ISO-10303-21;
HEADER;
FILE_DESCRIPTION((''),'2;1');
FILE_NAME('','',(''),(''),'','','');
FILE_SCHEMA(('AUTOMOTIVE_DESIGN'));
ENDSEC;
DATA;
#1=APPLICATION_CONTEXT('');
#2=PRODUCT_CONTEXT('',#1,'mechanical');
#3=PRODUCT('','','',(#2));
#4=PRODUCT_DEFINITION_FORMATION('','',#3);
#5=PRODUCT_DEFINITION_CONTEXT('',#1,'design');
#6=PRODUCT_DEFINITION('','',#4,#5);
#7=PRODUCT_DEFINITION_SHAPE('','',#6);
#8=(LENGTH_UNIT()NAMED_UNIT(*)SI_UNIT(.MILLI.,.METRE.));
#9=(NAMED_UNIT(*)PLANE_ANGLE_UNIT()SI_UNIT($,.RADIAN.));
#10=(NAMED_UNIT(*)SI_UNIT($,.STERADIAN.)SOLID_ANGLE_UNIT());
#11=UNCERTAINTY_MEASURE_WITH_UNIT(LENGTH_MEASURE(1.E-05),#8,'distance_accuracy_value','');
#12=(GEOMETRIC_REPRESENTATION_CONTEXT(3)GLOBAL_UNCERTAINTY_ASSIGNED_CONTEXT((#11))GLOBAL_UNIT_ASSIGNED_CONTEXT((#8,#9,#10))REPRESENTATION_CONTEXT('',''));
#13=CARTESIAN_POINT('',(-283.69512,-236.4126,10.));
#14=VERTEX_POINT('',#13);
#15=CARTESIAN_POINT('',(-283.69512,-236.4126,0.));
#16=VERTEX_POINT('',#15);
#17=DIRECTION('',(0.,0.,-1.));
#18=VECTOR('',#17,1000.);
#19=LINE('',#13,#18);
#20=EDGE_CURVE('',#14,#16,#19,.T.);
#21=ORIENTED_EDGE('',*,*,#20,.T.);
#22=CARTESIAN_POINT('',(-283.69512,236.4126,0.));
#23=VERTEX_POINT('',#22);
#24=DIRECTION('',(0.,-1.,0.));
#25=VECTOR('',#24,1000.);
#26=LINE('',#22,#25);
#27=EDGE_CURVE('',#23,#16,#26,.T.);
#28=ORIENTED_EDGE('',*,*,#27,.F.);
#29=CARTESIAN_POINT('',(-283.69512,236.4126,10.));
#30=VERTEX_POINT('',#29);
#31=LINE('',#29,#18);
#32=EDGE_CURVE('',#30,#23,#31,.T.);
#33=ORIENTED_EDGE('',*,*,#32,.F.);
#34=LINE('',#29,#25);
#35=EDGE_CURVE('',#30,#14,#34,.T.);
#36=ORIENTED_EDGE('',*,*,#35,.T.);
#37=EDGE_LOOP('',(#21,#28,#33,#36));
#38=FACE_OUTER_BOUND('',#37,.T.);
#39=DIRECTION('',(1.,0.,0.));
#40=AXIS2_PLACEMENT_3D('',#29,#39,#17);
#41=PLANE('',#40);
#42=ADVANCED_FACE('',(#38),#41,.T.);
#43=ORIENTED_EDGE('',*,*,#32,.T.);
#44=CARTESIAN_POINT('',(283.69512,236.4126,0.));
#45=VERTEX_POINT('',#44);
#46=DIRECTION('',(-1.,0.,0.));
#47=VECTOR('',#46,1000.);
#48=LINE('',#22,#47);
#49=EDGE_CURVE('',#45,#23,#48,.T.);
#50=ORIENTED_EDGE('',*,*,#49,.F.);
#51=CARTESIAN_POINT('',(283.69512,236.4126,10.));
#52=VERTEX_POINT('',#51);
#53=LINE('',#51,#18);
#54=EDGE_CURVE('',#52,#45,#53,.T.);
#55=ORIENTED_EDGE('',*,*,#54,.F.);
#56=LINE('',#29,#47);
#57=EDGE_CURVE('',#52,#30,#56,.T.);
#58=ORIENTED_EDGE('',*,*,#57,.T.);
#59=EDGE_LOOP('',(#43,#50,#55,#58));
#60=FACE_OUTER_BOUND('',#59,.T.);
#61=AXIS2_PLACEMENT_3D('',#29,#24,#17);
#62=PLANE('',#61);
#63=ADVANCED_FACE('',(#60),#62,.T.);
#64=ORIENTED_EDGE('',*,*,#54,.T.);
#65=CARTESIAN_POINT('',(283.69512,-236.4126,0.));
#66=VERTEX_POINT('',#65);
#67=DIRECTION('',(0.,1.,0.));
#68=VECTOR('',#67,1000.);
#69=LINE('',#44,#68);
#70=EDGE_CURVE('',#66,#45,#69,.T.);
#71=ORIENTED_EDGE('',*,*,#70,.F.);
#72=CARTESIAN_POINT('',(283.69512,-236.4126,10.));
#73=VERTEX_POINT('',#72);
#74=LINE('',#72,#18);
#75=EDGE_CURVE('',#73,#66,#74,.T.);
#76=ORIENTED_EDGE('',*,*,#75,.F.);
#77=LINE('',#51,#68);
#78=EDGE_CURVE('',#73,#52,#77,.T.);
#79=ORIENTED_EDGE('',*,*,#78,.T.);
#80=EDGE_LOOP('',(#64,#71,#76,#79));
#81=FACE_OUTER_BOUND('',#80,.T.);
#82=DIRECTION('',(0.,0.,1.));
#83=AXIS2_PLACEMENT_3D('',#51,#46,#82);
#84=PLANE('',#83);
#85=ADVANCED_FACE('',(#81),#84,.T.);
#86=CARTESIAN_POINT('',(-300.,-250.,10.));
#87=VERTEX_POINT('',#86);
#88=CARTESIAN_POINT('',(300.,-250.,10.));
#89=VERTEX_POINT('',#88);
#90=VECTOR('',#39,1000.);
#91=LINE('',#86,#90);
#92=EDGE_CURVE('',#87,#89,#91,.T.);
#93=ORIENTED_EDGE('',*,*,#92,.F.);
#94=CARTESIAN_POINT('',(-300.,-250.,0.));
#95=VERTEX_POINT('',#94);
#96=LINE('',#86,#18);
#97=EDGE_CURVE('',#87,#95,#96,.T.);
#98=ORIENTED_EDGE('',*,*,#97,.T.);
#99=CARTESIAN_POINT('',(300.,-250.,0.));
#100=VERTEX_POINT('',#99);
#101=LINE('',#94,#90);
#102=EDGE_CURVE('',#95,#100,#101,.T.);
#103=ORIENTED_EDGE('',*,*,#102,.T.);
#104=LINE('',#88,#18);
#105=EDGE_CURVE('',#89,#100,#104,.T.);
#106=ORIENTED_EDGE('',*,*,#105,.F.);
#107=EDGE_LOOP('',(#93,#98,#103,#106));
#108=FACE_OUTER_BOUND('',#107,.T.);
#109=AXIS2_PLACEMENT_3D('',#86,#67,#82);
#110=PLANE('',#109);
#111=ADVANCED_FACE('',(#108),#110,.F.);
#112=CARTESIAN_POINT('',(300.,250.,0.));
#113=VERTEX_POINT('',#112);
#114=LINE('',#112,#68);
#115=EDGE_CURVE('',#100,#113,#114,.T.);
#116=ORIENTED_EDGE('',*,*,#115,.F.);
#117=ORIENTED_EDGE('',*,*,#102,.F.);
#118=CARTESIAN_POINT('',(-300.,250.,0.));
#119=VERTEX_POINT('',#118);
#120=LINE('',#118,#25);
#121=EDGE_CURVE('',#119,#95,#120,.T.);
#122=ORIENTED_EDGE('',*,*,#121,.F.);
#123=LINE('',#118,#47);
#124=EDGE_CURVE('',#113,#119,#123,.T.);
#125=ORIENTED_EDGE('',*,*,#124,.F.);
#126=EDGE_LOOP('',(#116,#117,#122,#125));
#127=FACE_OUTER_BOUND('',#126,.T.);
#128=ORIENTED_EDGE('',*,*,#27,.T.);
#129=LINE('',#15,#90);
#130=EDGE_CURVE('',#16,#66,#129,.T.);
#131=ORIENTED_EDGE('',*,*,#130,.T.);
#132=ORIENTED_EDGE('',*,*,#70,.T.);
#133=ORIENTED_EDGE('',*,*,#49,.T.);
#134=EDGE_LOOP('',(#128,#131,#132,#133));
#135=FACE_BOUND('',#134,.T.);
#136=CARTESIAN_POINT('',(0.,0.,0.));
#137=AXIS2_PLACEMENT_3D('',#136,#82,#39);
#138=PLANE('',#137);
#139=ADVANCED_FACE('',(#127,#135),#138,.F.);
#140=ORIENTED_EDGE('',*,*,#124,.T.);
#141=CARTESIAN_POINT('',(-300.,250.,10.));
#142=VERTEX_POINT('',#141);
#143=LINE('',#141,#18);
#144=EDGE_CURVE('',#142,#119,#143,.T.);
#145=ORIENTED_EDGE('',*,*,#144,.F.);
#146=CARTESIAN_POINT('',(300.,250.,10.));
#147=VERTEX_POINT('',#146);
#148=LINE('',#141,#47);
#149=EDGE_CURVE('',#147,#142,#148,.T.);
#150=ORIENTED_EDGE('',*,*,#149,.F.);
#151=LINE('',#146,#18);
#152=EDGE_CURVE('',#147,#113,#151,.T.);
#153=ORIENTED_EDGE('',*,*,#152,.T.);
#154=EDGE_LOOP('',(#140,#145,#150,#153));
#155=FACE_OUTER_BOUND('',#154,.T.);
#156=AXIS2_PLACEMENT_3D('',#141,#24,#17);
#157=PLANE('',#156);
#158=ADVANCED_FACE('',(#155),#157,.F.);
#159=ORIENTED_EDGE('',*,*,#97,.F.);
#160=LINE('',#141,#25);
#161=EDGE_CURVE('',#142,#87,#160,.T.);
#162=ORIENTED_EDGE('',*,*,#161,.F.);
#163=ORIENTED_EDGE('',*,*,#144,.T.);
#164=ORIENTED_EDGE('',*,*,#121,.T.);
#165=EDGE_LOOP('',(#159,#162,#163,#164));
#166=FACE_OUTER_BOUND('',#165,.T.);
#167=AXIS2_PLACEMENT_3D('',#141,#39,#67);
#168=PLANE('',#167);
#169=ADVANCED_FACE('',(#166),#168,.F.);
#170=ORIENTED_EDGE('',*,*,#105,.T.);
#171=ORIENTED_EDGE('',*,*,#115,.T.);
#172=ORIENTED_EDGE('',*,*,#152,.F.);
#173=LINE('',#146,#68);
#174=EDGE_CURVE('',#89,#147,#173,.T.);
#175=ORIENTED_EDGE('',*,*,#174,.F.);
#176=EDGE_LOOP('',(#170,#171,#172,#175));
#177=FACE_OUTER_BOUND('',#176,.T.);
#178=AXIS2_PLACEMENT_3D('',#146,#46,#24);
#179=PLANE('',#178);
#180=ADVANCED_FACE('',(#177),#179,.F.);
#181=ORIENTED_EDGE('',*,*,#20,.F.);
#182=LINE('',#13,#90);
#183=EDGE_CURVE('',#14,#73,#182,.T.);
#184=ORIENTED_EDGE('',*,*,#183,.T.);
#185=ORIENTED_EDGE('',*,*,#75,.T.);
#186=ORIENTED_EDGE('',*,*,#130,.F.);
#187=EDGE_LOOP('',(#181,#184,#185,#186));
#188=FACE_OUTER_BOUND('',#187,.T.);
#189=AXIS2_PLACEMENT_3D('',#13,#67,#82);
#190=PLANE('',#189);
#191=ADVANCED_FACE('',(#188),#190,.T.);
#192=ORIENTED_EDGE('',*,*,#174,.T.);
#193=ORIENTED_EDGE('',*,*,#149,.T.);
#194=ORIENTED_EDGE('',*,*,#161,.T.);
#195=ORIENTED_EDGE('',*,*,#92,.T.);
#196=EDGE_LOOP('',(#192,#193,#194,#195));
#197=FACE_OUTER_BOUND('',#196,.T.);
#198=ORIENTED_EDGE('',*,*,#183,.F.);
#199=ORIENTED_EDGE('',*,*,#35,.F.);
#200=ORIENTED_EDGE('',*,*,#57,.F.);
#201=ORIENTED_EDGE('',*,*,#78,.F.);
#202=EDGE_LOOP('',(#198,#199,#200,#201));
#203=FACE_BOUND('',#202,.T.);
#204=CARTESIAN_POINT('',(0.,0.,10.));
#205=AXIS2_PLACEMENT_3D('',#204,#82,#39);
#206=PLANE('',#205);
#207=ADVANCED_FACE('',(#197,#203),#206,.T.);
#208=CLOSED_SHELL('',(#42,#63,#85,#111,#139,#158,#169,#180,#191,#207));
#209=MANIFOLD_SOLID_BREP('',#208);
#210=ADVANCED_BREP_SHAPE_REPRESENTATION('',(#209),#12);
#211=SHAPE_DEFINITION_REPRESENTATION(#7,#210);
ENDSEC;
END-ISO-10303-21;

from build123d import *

# Parameters (mm, degrees)
SKETCH1_W           = 600
SKETCH1_H           = 500
SKETCH1_W_2         = 567.390239782
SKETCH1_H_2         = 472.825199818
BOSS_EXTRUDE1_DEPTH = 10


with BuildPart() as part:
    # Sketch1 → Boss-Extrude1 (new body)
    with BuildSketch(Plane.XY):
        Rectangle(SKETCH1_W, SKETCH1_H)
        Rectangle(SKETCH1_W_2, SKETCH1_H_2, mode=Mode.SUBTRACT)
    extrude(amount=BOSS_EXTRUDE1_DEPTH)


solid = part.part
